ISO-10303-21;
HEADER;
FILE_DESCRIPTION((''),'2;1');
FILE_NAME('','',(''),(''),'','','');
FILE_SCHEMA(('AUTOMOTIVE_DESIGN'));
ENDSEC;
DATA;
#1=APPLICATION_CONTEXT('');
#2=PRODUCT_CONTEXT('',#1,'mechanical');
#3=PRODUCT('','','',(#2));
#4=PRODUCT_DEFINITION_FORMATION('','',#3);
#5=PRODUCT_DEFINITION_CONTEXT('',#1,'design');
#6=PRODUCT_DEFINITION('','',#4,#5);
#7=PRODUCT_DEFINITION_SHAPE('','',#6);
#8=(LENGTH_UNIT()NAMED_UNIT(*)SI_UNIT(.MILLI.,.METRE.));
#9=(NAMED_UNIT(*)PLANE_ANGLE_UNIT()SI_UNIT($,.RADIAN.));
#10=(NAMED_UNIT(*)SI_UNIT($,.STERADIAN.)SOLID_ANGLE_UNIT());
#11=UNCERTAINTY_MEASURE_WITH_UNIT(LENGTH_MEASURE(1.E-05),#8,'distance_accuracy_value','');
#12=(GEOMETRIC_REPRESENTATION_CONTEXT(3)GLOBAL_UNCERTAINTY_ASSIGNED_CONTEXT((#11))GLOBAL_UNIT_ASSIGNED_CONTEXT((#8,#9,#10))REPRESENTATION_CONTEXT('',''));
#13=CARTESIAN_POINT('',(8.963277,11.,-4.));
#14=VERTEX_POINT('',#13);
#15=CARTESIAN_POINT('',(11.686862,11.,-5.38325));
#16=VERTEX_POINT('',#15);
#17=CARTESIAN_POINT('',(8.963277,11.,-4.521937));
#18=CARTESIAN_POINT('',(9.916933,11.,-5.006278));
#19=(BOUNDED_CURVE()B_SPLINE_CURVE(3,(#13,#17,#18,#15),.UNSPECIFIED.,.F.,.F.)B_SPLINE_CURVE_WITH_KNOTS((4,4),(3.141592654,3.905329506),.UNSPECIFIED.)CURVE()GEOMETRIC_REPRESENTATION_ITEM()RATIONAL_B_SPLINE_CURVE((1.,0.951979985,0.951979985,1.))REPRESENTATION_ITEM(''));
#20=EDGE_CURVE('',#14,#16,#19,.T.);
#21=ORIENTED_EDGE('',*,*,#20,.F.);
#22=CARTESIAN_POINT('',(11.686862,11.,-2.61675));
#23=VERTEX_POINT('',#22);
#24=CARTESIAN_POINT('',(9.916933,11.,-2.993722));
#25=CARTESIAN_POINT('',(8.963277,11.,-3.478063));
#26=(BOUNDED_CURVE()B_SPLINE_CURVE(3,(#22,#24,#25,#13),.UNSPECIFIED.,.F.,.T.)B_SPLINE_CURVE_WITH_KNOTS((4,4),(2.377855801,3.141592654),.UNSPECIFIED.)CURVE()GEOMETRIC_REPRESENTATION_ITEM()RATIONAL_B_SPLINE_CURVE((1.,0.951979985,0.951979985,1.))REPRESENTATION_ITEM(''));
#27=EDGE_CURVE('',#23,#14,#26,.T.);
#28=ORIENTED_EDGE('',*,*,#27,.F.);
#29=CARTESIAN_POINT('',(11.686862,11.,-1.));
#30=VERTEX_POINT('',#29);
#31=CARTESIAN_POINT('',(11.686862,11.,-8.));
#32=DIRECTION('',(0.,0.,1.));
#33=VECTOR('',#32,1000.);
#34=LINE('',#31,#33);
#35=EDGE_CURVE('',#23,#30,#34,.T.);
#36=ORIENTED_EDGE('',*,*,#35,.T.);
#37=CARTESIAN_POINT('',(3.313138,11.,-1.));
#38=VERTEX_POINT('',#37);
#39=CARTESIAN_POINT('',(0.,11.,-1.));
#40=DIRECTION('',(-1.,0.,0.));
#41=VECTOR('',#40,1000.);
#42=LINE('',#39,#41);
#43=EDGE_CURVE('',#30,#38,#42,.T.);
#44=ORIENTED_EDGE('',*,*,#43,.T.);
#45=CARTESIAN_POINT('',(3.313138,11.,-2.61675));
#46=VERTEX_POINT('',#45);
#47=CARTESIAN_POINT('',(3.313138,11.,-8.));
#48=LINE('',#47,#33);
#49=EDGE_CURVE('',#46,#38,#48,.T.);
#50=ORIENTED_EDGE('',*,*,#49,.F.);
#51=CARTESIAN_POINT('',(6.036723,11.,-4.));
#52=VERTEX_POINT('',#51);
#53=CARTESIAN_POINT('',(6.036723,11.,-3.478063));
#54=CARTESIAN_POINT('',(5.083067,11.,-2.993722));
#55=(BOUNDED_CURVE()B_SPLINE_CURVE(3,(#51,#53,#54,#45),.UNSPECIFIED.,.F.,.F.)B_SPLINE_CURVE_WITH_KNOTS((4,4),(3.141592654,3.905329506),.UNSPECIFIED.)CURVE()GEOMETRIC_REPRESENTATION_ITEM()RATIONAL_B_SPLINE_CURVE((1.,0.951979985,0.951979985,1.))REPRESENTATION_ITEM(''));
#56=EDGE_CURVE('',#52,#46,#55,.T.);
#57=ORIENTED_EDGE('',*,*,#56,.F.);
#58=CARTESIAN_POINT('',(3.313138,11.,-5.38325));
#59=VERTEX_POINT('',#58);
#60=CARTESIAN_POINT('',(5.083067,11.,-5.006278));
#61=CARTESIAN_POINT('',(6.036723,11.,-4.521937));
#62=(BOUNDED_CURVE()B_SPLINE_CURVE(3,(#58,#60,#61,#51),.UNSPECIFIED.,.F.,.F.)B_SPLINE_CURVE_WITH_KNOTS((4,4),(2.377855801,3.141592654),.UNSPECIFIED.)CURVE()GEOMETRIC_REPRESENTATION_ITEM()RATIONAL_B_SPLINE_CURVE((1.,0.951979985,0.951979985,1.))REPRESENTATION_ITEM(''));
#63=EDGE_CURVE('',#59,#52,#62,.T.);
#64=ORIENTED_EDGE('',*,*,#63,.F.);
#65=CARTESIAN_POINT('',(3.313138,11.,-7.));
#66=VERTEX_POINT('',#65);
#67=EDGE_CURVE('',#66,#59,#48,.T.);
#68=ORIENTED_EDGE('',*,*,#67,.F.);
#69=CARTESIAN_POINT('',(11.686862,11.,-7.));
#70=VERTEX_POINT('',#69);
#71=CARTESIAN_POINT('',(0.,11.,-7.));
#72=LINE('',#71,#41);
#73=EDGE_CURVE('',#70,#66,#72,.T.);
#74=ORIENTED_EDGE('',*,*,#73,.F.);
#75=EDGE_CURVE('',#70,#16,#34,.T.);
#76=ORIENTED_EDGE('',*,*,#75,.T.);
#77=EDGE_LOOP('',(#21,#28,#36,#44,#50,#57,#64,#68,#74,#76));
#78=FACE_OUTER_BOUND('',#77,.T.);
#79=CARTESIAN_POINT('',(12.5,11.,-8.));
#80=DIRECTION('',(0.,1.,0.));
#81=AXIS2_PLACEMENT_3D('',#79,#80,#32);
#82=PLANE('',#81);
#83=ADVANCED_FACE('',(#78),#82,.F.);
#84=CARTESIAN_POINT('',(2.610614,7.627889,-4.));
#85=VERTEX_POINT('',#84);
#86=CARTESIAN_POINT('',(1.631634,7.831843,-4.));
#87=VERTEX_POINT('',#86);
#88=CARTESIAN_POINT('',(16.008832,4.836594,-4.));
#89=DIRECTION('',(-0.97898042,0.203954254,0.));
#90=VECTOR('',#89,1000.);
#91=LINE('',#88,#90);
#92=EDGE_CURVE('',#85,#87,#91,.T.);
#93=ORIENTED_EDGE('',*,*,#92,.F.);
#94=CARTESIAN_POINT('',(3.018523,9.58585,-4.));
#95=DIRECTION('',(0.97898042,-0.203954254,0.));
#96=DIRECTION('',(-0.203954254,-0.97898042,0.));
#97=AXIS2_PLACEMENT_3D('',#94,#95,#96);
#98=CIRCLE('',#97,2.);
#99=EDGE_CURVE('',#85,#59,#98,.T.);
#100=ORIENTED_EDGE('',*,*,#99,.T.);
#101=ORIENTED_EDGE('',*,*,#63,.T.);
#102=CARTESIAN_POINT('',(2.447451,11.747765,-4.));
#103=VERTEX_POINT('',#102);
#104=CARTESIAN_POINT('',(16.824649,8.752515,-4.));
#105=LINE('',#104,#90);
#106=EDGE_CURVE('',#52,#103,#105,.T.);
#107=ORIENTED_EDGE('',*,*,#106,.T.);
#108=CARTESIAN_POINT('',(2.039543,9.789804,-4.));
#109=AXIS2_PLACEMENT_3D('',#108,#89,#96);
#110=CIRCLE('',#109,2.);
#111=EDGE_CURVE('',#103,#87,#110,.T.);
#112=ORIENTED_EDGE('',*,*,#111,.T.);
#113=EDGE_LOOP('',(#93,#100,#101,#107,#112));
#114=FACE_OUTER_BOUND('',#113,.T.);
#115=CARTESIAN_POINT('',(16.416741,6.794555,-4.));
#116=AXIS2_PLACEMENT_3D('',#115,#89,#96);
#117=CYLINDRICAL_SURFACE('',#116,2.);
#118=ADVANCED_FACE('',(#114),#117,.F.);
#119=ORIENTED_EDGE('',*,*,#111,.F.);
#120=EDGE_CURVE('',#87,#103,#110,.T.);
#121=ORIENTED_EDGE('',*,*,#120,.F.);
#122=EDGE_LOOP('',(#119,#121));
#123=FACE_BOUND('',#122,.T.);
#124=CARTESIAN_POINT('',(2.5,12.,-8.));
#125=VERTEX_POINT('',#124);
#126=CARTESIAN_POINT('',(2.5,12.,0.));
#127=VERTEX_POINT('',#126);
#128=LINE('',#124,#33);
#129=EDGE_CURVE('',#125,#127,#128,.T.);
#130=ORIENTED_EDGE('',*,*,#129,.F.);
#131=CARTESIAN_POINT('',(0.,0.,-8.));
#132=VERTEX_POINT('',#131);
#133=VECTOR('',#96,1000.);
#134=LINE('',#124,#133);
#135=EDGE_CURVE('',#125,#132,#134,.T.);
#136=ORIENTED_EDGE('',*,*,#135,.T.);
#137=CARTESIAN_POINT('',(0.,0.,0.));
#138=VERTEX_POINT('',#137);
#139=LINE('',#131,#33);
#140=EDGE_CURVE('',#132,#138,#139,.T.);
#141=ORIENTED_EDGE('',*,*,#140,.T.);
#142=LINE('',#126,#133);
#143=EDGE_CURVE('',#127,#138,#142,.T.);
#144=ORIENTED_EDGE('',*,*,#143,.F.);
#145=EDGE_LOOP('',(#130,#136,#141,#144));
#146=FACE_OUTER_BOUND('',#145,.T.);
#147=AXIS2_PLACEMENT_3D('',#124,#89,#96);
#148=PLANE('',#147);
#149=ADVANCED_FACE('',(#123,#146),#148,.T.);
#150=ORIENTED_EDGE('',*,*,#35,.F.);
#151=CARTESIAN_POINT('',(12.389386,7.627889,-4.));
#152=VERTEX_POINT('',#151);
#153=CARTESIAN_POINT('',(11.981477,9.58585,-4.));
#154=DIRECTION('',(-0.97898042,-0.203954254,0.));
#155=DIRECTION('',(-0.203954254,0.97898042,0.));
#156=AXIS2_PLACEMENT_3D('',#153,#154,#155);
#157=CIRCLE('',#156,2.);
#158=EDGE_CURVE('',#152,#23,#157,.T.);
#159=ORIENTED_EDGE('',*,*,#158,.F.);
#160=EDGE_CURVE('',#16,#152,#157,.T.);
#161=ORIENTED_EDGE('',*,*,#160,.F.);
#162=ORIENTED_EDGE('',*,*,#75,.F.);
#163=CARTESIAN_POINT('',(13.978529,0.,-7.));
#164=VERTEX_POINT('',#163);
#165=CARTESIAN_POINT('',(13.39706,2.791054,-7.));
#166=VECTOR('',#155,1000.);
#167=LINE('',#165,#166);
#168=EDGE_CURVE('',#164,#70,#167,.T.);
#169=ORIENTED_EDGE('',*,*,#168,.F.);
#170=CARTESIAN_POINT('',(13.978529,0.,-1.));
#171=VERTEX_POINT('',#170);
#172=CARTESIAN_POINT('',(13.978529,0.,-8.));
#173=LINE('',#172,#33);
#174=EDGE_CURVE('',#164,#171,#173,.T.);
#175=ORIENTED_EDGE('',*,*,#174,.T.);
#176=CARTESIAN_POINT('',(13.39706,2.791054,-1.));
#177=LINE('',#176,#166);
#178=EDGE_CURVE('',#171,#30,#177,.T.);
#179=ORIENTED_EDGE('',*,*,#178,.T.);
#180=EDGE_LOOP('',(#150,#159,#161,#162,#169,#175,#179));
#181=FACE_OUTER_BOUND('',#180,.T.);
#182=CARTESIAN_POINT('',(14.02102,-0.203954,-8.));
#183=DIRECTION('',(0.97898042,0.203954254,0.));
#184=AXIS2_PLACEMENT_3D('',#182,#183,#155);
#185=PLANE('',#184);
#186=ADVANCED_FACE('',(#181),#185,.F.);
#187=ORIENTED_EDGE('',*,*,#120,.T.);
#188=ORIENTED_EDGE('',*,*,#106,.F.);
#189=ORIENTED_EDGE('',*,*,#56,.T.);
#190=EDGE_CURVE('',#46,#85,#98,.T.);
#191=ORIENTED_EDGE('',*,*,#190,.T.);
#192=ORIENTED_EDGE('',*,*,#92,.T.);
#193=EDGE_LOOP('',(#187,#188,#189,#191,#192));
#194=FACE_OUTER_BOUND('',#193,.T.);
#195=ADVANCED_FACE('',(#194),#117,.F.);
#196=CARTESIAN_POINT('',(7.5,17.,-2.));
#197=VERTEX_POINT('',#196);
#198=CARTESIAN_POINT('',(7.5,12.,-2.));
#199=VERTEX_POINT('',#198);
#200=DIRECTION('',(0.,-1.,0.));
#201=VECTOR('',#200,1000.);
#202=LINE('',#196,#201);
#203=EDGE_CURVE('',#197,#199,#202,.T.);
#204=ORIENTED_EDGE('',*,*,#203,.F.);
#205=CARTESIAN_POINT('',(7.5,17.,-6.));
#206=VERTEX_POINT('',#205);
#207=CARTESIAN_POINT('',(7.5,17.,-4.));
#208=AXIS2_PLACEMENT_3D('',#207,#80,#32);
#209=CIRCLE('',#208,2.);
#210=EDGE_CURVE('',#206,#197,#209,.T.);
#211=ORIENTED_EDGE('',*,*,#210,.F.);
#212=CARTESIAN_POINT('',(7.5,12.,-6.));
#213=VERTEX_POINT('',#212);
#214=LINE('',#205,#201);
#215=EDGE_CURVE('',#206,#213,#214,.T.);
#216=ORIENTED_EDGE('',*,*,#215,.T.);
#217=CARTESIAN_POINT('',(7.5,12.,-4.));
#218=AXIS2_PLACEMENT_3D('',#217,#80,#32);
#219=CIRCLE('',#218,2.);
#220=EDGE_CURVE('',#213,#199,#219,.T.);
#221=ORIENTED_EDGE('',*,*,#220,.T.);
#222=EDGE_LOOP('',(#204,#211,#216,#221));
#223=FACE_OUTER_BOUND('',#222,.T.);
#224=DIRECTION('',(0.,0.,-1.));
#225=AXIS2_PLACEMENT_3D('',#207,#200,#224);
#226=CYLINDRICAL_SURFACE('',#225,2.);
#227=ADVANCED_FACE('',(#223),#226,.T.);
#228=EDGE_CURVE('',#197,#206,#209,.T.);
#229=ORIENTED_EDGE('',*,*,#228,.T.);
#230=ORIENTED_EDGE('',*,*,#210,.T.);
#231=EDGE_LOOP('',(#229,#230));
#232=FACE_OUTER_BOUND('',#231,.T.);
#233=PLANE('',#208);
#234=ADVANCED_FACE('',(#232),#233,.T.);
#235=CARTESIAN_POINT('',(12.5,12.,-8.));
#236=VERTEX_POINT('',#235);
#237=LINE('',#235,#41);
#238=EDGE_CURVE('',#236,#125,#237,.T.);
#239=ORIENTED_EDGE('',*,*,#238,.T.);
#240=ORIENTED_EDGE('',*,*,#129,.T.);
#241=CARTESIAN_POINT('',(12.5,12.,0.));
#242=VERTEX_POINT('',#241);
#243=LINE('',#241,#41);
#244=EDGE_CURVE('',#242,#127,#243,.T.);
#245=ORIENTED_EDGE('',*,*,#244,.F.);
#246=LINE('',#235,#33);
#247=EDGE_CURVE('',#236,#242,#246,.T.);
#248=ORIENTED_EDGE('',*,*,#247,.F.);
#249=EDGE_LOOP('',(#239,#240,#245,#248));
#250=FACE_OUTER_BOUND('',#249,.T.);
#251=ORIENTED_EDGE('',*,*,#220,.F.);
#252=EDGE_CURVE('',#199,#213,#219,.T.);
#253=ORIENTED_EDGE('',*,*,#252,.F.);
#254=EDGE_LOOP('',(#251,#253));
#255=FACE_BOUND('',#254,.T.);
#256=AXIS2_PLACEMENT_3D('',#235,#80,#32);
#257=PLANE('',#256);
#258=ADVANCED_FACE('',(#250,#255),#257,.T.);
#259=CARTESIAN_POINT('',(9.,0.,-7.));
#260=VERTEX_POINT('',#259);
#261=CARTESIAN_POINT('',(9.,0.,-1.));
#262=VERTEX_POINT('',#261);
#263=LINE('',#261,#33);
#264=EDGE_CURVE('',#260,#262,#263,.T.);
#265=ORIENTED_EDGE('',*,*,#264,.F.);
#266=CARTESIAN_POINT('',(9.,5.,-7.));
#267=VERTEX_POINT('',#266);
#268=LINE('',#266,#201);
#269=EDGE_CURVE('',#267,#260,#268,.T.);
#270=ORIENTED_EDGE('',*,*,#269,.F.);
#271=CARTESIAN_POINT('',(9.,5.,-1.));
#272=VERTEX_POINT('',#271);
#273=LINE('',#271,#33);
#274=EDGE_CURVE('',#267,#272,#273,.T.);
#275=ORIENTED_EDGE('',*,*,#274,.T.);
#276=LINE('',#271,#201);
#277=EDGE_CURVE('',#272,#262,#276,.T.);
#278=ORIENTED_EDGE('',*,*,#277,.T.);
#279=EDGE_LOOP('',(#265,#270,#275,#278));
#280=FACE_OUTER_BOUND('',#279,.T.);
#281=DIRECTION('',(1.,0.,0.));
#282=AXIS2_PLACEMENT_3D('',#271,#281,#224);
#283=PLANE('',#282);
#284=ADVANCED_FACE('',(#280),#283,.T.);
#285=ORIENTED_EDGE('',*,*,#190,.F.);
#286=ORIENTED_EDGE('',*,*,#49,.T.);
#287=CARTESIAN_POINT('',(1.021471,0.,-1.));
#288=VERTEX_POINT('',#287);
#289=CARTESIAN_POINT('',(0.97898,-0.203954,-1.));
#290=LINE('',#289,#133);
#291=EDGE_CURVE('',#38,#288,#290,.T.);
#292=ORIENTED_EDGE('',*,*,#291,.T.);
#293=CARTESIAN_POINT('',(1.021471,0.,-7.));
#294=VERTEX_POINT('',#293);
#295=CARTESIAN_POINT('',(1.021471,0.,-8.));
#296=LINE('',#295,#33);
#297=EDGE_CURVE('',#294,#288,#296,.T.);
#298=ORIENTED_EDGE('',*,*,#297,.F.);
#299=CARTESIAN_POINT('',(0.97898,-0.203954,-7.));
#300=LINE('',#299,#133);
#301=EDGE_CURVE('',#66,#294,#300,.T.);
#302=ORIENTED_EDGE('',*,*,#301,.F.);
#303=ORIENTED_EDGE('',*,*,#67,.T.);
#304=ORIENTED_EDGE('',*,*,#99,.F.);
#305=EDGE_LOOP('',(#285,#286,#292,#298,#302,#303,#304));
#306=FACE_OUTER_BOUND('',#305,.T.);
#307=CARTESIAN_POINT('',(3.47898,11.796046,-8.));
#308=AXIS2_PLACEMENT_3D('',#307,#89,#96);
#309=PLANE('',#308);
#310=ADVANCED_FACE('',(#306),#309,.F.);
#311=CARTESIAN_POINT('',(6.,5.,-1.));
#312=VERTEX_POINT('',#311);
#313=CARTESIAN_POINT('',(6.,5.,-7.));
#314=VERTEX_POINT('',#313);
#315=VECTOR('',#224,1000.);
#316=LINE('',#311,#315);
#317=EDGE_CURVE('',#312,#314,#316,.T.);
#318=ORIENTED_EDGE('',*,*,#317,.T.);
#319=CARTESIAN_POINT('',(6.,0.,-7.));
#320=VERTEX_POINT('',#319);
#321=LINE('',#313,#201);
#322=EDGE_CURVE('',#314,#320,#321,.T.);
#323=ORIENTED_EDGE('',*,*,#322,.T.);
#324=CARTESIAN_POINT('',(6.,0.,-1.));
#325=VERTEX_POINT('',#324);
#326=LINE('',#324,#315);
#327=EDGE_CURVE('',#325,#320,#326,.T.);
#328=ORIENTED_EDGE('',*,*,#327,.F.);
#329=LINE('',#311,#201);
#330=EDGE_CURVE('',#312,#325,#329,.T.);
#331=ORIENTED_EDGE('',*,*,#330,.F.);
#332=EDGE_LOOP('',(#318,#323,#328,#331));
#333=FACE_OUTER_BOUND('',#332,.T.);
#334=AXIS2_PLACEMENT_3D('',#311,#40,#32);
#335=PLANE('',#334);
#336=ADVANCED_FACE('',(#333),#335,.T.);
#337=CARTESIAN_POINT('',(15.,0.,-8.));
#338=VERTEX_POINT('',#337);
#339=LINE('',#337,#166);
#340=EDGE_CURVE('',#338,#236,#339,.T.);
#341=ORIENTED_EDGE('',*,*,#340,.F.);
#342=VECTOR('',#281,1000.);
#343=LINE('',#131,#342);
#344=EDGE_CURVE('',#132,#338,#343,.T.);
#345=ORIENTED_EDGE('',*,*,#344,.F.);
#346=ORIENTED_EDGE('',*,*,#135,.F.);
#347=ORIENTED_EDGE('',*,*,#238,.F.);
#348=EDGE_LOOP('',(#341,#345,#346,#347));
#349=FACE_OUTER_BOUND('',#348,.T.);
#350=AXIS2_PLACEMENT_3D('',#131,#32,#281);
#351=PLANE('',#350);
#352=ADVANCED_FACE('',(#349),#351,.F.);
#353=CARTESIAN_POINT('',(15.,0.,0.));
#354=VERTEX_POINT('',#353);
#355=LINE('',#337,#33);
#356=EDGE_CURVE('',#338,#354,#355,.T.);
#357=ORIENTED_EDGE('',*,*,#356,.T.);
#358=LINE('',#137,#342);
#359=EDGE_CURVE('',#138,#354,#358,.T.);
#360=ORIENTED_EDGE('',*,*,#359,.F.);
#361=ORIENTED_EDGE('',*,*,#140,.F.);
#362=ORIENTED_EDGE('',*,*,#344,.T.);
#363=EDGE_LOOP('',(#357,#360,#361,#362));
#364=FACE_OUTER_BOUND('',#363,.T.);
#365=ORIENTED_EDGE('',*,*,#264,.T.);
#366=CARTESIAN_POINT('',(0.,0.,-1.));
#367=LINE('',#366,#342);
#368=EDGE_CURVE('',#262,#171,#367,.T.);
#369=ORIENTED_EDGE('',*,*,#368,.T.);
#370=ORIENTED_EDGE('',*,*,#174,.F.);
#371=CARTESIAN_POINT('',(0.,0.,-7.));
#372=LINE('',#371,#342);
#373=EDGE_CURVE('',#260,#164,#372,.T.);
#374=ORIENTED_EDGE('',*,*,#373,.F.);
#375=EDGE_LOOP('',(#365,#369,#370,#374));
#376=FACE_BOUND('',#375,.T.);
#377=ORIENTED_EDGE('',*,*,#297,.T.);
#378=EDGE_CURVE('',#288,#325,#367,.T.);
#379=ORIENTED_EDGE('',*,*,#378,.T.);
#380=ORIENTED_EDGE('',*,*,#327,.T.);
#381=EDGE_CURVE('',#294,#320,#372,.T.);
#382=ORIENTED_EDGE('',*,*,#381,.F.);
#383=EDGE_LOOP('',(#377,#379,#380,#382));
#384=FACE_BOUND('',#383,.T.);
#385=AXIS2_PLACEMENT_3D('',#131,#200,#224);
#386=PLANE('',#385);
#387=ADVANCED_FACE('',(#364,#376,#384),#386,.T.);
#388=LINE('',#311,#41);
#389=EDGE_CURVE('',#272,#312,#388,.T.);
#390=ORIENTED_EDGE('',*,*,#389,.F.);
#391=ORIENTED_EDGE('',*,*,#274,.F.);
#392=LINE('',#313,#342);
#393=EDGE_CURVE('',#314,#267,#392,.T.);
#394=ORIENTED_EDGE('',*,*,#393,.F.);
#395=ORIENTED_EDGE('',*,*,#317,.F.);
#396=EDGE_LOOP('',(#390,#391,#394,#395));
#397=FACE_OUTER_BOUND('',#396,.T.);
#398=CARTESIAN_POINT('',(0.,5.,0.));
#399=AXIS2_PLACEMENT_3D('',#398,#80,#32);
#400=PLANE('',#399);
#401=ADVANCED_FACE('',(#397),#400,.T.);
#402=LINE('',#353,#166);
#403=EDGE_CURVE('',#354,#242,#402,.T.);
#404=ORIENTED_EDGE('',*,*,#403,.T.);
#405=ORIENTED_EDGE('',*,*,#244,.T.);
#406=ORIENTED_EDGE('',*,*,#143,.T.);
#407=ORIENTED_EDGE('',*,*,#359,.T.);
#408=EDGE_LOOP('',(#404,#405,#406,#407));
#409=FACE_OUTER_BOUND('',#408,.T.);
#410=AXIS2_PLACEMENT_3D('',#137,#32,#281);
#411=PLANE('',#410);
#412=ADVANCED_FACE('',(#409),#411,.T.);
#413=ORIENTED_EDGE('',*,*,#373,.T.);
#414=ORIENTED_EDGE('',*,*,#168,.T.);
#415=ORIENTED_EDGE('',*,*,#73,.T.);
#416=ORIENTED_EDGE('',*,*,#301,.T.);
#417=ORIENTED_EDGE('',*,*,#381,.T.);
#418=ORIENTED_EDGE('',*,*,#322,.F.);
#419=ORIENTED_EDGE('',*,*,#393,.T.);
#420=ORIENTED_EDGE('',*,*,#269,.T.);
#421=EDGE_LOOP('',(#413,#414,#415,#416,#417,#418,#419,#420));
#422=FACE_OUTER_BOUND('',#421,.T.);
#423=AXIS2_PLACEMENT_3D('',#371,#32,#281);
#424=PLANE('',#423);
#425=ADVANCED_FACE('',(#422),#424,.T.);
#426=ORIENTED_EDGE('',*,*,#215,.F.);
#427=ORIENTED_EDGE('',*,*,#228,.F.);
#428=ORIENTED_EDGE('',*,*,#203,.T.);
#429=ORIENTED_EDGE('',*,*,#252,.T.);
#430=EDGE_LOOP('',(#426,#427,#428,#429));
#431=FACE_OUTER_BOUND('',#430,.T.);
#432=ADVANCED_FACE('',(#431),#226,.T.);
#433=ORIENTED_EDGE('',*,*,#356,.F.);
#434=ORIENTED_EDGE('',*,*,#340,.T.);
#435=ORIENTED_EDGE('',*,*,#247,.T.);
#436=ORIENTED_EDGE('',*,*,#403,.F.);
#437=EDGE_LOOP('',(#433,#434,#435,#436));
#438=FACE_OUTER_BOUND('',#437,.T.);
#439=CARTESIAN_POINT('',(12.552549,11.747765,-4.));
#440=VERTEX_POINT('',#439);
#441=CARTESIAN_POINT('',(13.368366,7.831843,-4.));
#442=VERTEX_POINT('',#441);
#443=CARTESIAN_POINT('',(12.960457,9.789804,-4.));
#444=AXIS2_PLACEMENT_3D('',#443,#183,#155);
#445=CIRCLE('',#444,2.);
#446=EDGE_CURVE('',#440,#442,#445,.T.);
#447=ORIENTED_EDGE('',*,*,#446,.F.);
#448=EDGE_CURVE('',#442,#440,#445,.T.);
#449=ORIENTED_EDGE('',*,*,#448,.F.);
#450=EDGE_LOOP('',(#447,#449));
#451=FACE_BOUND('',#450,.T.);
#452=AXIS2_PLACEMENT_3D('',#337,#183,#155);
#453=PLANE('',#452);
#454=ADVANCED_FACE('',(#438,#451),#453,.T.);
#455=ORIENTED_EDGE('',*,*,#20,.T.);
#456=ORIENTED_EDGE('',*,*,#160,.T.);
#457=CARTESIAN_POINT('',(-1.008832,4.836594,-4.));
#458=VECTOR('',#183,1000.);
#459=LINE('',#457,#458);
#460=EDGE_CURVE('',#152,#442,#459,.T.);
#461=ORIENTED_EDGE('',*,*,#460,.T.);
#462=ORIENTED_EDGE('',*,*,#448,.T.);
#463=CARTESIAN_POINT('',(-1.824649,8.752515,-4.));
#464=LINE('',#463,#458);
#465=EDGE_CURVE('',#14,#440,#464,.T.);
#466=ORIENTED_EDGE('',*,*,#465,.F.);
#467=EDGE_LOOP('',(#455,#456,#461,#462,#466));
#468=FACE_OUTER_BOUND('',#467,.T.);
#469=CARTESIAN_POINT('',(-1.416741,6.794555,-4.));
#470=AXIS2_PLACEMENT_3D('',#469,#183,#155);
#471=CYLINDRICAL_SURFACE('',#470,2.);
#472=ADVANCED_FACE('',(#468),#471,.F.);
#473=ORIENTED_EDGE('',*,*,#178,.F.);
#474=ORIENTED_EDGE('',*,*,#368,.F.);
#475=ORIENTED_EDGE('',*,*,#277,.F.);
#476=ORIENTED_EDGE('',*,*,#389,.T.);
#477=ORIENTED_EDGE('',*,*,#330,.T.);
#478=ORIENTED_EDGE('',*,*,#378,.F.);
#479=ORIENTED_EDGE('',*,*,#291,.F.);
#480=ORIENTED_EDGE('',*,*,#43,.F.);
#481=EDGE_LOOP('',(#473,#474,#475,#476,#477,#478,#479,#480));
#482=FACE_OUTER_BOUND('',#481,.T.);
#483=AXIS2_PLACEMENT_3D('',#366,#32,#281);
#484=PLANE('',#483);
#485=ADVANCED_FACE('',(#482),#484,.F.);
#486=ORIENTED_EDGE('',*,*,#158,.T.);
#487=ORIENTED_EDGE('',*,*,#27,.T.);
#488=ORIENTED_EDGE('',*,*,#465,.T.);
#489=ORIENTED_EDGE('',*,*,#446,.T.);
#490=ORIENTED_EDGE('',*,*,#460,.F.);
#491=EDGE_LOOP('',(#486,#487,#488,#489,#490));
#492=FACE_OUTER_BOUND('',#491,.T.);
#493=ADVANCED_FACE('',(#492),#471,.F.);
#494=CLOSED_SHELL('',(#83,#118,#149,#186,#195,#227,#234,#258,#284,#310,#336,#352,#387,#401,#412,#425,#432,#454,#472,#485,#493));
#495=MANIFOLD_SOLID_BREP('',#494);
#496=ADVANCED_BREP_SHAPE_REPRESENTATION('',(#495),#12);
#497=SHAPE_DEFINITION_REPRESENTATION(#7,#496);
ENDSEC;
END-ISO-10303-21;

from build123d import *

# Parameters (mm, degrees)
TORSO_BLOCK_DEPTH        = 8
TORSO_SHELL_1MM_T        = -1
NECK_STUD_SKETCH_R       = 2
NECK_STUD_4_DEPTH        = 5
ARM_HOLE_1_3_REACH       = 23.606
ARM_HOLE_1_SKETCH_R      = 2
ARM_HOLE_2_3_REACH       = 26.042
ARM_HOLE_2_SKETCH_R      = 2
HIP_CONNECTOR_SKETCH_W   = 3
HIP_CONNECTOR_SKETCH_H   = 6
HIP_CONNECTOR_BOSS_DEPTH = 5


with BuildPart() as part:
    # Torso Profile Sketch → Torso Block (new body)
    with BuildSketch(Plane.XY):
        Polygon((0, 0), (15, 0), (12.5, 12), (2.5, 12), align=None)
    extrude(amount=-TORSO_BLOCK_DEPTH)

    # Torso Shell 1mm
    torso_shell_1mm_openings = [part.faces().sort_by_distance(p)[0] for p in [
        (7.5, 0, -4),
    ]]
    offset(amount=TORSO_SHELL_1MM_T, openings=torso_shell_1mm_openings, kind=Kind.INTERSECTION)

    # Neck Stud Sketch → Neck Stud Ø4 (add)
    with BuildSketch(Plane(origin=(0, 12, 0), x_dir=(1, 0, 0), z_dir=(0, 1, 0))):
        with Locations(Location((7.5, 4, 0), (0, 0, 270))):
            Circle(NECK_STUD_SKETCH_R)
    extrude(amount=NECK_STUD_4_DEPTH)

    # Arm Hole 1 Sketch → Arm Hole 1 Ø3 (cut, up to next)
    with BuildSketch(Plane(origin=(14.376039933, 2.995008319, 0), x_dir=(0, 0, -1), z_dir=(0.978980419737605, 0.20395425411200113, 0)), mode=Mode.PRIVATE) as arm_hole_1_3_sk1:
        with Locations(Location((4, 6.940686188, 0), (0, 0, 90))):
            Circle(ARM_HOLE_1_SKETCH_R)
    arm_hole_1_3_tool1 = extrude(arm_hole_1_3_sk1.sketch, amount=-ARM_HOLE_1_3_REACH, mode=Mode.PRIVATE) & part.part
    add(arm_hole_1_3_tool1.solids().sort_by_distance((12.960457, 9.789804, -4))[0], mode=Mode.SUBTRACT)

    # Arm Hole 2 Sketch → Arm Hole 2 Ø3 (cut, up to next)
    with BuildSketch(Plane(origin=(0, 0, 0), x_dir=(0, 0, 1), z_dir=(-0.978980419737605, 0.20395425411200113, 0)), mode=Mode.PRIVATE) as arm_hole_2_3_sk1:
        with Locations(Location((-4, 10, 0), (0, 0, 270))):
            Circle(ARM_HOLE_2_SKETCH_R)
    arm_hole_2_3_tool1 = extrude(arm_hole_2_3_sk1.sketch, amount=-ARM_HOLE_2_3_REACH, mode=Mode.PRIVATE) & part.part
    add(arm_hole_2_3_tool1.solids().sort_by_distance((2.039543, 9.789804, -4))[0], mode=Mode.SUBTRACT)

    # Hip Connector Sketch → Hip Connector Boss (add)
    with BuildSketch(Plane.XZ):
        with Locations((7.5, -4)):
            Rectangle(HIP_CONNECTOR_SKETCH_W, HIP_CONNECTOR_SKETCH_H)
    extrude(amount=-HIP_CONNECTOR_BOSS_DEPTH)


solid = part.part
